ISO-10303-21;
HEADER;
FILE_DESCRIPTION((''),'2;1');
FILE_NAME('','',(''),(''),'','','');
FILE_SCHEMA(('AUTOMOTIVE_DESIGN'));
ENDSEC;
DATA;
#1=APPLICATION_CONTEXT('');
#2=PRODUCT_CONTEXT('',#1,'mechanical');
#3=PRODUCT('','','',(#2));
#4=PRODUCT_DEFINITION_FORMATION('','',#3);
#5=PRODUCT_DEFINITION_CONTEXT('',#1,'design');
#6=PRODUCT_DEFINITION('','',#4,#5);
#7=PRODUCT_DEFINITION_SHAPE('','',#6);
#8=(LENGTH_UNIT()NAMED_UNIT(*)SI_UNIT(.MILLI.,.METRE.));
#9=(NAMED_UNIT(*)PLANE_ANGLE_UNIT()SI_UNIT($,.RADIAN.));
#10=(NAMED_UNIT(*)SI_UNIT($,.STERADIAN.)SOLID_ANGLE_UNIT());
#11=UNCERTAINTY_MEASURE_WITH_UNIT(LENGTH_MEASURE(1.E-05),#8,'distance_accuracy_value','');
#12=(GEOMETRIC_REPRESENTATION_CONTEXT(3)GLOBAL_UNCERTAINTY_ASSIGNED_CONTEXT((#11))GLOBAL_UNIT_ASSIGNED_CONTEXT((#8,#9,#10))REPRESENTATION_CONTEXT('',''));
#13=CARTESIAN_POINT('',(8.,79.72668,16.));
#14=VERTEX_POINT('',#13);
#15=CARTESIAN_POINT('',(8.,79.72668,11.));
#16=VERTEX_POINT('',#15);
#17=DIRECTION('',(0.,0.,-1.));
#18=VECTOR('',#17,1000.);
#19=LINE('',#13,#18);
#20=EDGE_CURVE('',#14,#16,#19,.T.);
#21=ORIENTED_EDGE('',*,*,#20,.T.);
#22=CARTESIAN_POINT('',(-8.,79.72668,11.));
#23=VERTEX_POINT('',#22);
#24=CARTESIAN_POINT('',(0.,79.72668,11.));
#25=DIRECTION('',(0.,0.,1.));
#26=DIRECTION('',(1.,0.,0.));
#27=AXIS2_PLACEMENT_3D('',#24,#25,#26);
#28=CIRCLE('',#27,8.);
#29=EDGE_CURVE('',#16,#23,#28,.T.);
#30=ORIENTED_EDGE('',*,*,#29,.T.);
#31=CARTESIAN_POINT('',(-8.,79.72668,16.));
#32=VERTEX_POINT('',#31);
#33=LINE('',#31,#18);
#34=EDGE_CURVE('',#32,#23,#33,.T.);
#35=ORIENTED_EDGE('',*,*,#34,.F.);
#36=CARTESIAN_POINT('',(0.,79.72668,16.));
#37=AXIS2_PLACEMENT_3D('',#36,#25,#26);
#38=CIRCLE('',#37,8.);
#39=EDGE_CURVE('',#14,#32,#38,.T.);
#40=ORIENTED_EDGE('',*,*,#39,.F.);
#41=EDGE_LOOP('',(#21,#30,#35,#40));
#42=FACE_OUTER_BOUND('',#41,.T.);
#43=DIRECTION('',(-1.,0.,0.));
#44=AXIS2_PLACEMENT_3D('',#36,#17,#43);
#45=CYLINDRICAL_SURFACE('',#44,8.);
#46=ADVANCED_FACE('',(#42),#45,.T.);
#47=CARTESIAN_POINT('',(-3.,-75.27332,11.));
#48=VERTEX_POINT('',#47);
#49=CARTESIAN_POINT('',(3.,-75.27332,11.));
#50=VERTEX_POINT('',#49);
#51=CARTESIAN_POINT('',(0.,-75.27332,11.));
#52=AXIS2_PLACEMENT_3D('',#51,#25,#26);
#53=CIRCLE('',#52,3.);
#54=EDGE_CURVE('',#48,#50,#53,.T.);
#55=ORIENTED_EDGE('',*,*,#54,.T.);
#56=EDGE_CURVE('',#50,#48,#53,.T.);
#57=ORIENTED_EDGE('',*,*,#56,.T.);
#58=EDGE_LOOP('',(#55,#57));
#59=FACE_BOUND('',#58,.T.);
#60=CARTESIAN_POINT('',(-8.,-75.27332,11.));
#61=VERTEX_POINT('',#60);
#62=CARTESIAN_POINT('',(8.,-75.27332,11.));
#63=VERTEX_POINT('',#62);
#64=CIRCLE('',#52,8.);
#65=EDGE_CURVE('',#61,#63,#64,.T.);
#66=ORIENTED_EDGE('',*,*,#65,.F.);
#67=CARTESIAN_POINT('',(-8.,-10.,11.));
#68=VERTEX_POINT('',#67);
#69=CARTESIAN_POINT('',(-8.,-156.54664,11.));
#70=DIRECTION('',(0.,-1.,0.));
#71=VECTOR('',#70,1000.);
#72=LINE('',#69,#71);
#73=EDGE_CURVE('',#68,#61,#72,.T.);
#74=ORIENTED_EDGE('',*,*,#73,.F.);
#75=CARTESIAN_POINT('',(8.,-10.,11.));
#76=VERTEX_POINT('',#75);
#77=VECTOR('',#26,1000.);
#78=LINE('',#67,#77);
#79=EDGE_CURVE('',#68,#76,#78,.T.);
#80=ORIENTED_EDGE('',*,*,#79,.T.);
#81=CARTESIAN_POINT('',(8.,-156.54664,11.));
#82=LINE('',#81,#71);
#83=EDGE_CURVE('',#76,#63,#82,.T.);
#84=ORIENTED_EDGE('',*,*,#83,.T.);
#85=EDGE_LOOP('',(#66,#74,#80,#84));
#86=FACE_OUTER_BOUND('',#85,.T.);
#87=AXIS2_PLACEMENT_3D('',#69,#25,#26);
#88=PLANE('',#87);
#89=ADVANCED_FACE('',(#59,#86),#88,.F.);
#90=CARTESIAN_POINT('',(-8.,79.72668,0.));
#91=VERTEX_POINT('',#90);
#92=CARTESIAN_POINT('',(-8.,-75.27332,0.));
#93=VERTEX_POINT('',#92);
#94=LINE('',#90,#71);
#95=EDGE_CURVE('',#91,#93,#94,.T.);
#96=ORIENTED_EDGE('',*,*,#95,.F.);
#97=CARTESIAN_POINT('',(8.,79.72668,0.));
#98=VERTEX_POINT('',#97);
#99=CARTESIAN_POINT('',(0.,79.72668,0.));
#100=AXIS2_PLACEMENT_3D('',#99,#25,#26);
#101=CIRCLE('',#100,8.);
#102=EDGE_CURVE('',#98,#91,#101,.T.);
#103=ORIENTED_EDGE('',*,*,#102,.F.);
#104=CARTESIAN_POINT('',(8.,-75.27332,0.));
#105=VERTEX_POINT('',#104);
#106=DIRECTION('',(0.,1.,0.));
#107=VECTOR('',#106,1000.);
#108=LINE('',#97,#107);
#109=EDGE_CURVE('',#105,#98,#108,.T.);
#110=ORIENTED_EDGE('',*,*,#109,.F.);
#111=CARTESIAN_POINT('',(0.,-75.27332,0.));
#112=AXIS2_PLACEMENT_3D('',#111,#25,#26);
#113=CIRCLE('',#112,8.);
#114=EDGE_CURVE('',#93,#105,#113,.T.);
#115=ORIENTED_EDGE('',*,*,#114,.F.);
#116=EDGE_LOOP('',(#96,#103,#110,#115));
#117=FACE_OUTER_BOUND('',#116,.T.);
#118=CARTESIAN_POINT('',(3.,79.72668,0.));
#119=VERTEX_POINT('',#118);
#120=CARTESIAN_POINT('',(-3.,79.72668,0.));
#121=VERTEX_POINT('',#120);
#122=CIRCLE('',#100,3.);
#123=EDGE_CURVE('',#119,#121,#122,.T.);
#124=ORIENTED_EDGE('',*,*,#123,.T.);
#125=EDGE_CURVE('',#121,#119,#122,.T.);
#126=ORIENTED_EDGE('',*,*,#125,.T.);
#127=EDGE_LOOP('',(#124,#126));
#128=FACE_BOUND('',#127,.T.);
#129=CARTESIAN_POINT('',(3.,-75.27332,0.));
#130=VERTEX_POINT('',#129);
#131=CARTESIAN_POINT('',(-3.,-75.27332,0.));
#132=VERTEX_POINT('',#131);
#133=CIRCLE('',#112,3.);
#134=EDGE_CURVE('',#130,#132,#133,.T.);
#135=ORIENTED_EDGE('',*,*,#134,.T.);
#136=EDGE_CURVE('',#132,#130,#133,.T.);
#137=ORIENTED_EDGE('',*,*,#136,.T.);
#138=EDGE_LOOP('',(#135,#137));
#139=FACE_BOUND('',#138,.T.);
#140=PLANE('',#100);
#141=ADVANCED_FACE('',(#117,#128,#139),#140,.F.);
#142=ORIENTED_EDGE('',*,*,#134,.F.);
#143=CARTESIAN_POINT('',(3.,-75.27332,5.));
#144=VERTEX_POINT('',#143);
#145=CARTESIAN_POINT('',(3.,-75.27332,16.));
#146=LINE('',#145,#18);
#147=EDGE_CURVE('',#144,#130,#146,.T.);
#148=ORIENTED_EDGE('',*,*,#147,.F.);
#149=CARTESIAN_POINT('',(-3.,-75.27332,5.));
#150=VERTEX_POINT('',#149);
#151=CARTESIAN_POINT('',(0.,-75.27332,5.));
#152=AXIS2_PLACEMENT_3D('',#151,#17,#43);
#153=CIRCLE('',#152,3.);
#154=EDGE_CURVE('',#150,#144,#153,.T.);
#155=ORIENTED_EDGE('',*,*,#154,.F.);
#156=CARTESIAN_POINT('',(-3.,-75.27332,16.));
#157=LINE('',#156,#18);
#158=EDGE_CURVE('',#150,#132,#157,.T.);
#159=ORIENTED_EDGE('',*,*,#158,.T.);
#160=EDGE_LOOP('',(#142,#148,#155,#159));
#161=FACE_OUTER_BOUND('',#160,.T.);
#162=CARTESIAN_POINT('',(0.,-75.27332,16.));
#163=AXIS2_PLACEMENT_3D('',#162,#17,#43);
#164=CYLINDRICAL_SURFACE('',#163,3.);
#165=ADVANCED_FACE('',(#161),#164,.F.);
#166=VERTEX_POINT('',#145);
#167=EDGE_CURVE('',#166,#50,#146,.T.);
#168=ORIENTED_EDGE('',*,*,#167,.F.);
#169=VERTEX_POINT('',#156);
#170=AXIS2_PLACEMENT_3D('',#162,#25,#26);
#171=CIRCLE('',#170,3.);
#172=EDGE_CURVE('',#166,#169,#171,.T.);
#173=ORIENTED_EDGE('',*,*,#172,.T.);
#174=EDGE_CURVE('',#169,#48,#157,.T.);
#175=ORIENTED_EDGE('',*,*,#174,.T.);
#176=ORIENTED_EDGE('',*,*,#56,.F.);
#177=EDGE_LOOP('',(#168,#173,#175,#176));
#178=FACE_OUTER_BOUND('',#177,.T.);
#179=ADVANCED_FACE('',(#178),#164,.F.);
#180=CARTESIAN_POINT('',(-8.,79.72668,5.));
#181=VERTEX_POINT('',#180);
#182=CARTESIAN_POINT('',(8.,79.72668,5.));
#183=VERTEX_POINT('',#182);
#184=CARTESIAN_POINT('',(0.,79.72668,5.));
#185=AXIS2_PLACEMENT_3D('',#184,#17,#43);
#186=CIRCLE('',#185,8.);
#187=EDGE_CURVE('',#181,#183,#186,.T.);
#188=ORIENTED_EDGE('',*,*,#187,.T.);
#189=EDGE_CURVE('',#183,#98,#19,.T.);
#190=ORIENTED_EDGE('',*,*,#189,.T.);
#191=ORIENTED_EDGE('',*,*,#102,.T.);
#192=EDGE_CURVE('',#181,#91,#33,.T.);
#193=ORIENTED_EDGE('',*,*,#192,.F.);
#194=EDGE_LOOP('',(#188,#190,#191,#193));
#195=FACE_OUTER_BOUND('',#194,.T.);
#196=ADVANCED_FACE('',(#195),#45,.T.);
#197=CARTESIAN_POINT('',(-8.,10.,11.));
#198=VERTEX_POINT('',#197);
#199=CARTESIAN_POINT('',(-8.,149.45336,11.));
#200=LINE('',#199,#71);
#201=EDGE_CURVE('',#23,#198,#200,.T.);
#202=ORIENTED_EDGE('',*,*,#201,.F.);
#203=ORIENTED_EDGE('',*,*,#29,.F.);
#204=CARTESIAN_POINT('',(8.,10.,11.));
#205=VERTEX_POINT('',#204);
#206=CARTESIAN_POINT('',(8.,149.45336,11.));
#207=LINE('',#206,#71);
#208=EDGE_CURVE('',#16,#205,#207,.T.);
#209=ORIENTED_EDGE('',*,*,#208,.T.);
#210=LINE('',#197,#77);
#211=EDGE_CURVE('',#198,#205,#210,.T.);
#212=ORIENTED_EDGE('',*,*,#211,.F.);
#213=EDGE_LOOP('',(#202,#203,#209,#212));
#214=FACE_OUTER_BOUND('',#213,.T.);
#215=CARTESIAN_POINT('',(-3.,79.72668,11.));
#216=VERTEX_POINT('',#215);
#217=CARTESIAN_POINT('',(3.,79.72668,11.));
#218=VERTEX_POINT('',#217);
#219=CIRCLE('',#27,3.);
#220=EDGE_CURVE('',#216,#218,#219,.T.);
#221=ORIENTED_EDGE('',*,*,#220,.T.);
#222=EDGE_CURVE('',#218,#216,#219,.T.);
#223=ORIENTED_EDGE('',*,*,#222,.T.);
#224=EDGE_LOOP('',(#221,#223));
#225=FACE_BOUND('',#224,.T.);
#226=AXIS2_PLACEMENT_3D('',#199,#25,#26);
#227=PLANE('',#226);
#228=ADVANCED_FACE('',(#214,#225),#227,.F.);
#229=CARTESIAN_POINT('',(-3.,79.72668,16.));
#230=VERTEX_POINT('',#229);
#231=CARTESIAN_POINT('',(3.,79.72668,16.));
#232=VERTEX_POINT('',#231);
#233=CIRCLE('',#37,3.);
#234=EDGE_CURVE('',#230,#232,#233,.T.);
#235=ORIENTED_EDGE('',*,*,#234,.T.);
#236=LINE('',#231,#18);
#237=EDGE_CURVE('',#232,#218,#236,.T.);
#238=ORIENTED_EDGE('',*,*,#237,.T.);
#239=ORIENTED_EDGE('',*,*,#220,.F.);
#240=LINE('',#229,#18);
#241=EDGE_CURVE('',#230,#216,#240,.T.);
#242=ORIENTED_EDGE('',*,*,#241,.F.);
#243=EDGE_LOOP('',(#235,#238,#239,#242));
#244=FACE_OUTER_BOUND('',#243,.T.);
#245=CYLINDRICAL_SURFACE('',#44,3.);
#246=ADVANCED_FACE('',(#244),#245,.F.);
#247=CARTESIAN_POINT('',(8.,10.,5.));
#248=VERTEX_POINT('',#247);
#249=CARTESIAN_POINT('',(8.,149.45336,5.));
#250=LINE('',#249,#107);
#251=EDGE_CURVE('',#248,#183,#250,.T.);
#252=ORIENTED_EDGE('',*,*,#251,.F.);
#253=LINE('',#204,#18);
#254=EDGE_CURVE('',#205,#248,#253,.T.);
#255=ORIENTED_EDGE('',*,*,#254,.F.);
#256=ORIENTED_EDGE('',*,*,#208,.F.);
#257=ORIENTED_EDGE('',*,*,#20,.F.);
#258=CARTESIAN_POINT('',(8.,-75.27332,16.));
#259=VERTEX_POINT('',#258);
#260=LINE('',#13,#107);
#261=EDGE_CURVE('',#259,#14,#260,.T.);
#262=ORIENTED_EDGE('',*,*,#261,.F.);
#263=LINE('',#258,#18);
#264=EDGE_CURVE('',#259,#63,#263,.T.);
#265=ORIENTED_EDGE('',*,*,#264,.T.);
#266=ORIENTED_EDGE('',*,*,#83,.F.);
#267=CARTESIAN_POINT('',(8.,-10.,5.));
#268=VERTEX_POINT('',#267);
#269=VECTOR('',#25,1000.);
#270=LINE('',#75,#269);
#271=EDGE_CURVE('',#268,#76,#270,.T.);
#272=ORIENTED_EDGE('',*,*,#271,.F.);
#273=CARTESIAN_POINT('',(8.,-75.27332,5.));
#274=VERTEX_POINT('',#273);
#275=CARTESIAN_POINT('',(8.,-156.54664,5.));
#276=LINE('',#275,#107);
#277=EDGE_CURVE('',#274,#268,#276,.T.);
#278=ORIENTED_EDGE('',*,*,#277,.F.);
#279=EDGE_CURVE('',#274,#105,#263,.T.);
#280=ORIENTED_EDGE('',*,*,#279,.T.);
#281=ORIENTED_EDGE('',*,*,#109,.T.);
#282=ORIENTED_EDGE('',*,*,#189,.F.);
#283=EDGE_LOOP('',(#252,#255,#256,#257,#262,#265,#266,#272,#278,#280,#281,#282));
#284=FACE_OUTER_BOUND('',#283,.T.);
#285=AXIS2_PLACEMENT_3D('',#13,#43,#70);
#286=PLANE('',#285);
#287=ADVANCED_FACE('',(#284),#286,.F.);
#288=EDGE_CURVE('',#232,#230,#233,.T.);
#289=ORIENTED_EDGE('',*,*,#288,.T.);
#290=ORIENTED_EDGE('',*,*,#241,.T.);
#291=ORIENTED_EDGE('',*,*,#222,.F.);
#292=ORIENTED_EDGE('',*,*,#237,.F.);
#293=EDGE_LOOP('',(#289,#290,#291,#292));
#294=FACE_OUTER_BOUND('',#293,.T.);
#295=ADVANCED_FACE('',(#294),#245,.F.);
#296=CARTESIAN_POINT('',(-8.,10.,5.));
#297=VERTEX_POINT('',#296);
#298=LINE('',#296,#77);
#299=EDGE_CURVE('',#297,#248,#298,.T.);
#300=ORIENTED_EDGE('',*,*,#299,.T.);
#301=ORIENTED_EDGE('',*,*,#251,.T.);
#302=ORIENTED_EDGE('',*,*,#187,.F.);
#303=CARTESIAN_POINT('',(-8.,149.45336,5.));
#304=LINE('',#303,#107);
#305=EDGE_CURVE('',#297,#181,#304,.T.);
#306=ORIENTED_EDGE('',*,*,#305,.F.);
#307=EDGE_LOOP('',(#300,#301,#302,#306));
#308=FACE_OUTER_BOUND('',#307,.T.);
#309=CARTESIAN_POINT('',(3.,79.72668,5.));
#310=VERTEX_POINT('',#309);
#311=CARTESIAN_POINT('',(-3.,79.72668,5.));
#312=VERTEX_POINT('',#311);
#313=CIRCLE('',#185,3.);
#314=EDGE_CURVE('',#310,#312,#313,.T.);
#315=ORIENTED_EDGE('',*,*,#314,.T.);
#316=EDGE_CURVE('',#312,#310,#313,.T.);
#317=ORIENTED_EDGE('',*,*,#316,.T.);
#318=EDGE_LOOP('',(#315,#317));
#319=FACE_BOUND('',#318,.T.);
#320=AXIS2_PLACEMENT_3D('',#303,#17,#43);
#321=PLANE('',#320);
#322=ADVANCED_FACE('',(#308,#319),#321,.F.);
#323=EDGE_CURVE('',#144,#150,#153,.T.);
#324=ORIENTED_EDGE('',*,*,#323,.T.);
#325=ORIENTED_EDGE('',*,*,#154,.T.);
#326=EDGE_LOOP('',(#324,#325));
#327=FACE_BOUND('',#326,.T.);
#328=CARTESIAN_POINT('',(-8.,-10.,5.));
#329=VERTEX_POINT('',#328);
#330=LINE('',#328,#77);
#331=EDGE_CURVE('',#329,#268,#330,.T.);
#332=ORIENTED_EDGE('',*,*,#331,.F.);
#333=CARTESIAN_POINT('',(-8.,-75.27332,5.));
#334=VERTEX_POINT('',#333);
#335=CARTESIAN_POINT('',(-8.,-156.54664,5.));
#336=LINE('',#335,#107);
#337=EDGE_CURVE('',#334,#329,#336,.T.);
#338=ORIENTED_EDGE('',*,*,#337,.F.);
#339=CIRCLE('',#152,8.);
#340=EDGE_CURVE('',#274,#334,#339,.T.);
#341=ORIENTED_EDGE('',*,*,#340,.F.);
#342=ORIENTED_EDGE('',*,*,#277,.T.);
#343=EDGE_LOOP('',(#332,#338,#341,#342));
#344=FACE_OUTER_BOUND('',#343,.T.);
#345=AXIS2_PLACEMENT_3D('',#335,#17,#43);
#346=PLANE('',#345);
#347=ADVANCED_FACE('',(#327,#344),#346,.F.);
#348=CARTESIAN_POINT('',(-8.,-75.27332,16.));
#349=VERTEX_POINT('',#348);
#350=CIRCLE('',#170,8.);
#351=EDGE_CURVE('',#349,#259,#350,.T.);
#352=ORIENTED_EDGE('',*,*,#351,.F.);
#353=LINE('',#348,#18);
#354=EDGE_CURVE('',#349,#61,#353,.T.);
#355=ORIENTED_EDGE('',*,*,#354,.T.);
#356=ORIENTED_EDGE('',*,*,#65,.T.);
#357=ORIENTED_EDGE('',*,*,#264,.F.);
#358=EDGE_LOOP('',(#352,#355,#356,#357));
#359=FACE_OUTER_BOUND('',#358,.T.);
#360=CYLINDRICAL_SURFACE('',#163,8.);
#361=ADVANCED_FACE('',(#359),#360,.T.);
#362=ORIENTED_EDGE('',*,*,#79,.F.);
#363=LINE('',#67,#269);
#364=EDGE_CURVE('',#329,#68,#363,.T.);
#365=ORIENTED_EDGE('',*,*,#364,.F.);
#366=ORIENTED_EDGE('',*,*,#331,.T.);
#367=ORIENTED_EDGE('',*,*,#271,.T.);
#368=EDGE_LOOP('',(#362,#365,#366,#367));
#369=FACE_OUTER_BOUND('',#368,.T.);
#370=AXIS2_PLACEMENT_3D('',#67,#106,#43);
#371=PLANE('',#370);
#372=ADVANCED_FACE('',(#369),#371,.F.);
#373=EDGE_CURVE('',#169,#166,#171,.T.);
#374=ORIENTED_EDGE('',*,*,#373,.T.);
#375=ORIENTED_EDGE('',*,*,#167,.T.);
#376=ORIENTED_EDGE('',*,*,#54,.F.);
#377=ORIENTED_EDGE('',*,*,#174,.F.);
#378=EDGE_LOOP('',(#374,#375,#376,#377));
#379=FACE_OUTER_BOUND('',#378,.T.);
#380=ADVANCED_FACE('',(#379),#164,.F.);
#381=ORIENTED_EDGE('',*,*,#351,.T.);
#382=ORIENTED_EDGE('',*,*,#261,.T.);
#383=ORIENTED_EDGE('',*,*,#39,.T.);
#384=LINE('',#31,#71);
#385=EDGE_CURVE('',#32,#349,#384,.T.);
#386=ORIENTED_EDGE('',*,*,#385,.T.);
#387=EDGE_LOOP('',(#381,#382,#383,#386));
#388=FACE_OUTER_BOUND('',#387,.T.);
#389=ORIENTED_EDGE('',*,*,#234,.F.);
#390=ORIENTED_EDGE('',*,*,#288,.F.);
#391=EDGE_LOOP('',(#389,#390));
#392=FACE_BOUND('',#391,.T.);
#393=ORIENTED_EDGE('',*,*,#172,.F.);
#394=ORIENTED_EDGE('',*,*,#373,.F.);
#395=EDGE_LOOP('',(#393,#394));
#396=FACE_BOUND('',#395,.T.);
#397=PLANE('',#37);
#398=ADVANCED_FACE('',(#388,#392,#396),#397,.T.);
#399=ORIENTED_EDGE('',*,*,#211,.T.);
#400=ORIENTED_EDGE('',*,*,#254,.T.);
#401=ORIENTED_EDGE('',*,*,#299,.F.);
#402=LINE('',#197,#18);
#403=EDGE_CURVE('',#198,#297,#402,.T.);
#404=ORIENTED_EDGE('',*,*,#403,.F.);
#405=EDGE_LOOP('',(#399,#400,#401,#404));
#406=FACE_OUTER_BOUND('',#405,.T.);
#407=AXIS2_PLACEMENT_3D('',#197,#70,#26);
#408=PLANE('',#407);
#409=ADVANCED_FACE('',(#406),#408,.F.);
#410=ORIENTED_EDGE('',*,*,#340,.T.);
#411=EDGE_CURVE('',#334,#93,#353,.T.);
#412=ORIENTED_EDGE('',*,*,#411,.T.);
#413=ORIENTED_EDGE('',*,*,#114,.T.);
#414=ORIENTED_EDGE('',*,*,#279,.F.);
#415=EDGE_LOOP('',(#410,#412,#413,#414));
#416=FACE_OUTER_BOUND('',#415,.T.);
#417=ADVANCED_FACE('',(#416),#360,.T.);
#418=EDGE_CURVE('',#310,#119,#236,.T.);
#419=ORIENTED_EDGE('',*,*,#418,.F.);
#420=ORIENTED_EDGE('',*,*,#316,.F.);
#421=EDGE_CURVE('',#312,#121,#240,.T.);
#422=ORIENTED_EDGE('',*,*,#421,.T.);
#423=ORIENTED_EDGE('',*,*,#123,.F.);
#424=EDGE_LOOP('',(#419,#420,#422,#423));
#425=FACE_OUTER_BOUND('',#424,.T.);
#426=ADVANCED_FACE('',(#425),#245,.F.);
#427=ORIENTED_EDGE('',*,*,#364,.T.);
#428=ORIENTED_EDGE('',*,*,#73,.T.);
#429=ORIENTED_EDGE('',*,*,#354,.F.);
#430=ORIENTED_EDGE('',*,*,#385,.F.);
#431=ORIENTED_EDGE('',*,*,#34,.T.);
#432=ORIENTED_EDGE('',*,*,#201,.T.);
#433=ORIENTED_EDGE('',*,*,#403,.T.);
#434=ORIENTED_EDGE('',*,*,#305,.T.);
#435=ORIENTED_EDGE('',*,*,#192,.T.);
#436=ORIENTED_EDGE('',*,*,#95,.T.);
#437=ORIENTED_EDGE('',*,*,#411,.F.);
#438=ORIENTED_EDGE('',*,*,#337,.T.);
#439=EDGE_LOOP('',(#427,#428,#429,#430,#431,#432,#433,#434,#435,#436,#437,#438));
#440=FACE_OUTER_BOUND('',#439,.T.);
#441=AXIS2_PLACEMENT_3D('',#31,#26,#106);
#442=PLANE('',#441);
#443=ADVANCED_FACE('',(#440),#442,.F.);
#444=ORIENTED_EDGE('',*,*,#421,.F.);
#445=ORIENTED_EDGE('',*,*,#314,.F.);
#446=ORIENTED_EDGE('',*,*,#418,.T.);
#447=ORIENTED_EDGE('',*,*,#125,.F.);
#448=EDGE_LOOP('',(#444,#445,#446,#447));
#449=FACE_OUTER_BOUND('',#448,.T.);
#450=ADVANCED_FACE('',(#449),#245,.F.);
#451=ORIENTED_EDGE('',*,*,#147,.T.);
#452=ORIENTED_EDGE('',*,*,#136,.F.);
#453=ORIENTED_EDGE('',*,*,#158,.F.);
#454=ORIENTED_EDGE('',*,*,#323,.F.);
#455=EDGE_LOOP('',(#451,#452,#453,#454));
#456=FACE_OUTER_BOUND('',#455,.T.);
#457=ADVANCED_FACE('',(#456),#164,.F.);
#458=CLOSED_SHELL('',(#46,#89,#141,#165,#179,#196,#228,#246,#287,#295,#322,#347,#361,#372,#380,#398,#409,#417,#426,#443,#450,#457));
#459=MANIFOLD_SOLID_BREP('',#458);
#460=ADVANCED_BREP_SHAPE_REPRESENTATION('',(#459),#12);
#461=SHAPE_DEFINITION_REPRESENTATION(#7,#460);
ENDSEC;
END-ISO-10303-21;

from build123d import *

# Parameters (mm, degrees)
SKETCH1_R           = 3
BOSS_EXTRUDE1_DEPTH = 16
SKETCH2_W           = 6
SKETCH2_H           = 139.453359721
SKETCH2_H_2         = 146.546640279
CUT_EXTRUDE1_DEPTH  = 91.59784964


with BuildPart() as part:
    # Sketch1 → Boss-Extrude1 (new body)
    with BuildSketch(Plane.XY):
        with BuildLine():
            Line((-8, 79.726679861), (-8, -75.273320139))
            ThreePointArc((-8, -75.273320139), (0, -83.273320139), (8, -75.273320139))
            Line((8, -75.273320139), (8, 79.726679861))
            ThreePointArc((8, 79.726679861), (0, 87.726679861), (-8, 79.726679861))
        make_face()
        with Locations((0, 79.726679861)):
            Circle(SKETCH1_R, mode=Mode.SUBTRACT)
        with Locations((0, -75.273320139)):
            Circle(SKETCH1_R, mode=Mode.SUBTRACT)
    extrude(amount=BOSS_EXTRUDE1_DEPTH)

    # Sketch2 → Cut-Extrude1 (cut, through all)
    with BuildSketch(Plane(origin=(8, 0, 0), x_dir=(0, 0, -1), z_dir=(1, 0, 0))):
        with Locations((-8, 79.72667986)):
            Rectangle(SKETCH2_W, SKETCH2_H)
        with Locations((-8, -83.27332014)):
            Rectangle(SKETCH2_W, SKETCH2_H_2)
    extrude(amount=-CUT_EXTRUDE1_DEPTH, mode=Mode.SUBTRACT)


solid = part.part
